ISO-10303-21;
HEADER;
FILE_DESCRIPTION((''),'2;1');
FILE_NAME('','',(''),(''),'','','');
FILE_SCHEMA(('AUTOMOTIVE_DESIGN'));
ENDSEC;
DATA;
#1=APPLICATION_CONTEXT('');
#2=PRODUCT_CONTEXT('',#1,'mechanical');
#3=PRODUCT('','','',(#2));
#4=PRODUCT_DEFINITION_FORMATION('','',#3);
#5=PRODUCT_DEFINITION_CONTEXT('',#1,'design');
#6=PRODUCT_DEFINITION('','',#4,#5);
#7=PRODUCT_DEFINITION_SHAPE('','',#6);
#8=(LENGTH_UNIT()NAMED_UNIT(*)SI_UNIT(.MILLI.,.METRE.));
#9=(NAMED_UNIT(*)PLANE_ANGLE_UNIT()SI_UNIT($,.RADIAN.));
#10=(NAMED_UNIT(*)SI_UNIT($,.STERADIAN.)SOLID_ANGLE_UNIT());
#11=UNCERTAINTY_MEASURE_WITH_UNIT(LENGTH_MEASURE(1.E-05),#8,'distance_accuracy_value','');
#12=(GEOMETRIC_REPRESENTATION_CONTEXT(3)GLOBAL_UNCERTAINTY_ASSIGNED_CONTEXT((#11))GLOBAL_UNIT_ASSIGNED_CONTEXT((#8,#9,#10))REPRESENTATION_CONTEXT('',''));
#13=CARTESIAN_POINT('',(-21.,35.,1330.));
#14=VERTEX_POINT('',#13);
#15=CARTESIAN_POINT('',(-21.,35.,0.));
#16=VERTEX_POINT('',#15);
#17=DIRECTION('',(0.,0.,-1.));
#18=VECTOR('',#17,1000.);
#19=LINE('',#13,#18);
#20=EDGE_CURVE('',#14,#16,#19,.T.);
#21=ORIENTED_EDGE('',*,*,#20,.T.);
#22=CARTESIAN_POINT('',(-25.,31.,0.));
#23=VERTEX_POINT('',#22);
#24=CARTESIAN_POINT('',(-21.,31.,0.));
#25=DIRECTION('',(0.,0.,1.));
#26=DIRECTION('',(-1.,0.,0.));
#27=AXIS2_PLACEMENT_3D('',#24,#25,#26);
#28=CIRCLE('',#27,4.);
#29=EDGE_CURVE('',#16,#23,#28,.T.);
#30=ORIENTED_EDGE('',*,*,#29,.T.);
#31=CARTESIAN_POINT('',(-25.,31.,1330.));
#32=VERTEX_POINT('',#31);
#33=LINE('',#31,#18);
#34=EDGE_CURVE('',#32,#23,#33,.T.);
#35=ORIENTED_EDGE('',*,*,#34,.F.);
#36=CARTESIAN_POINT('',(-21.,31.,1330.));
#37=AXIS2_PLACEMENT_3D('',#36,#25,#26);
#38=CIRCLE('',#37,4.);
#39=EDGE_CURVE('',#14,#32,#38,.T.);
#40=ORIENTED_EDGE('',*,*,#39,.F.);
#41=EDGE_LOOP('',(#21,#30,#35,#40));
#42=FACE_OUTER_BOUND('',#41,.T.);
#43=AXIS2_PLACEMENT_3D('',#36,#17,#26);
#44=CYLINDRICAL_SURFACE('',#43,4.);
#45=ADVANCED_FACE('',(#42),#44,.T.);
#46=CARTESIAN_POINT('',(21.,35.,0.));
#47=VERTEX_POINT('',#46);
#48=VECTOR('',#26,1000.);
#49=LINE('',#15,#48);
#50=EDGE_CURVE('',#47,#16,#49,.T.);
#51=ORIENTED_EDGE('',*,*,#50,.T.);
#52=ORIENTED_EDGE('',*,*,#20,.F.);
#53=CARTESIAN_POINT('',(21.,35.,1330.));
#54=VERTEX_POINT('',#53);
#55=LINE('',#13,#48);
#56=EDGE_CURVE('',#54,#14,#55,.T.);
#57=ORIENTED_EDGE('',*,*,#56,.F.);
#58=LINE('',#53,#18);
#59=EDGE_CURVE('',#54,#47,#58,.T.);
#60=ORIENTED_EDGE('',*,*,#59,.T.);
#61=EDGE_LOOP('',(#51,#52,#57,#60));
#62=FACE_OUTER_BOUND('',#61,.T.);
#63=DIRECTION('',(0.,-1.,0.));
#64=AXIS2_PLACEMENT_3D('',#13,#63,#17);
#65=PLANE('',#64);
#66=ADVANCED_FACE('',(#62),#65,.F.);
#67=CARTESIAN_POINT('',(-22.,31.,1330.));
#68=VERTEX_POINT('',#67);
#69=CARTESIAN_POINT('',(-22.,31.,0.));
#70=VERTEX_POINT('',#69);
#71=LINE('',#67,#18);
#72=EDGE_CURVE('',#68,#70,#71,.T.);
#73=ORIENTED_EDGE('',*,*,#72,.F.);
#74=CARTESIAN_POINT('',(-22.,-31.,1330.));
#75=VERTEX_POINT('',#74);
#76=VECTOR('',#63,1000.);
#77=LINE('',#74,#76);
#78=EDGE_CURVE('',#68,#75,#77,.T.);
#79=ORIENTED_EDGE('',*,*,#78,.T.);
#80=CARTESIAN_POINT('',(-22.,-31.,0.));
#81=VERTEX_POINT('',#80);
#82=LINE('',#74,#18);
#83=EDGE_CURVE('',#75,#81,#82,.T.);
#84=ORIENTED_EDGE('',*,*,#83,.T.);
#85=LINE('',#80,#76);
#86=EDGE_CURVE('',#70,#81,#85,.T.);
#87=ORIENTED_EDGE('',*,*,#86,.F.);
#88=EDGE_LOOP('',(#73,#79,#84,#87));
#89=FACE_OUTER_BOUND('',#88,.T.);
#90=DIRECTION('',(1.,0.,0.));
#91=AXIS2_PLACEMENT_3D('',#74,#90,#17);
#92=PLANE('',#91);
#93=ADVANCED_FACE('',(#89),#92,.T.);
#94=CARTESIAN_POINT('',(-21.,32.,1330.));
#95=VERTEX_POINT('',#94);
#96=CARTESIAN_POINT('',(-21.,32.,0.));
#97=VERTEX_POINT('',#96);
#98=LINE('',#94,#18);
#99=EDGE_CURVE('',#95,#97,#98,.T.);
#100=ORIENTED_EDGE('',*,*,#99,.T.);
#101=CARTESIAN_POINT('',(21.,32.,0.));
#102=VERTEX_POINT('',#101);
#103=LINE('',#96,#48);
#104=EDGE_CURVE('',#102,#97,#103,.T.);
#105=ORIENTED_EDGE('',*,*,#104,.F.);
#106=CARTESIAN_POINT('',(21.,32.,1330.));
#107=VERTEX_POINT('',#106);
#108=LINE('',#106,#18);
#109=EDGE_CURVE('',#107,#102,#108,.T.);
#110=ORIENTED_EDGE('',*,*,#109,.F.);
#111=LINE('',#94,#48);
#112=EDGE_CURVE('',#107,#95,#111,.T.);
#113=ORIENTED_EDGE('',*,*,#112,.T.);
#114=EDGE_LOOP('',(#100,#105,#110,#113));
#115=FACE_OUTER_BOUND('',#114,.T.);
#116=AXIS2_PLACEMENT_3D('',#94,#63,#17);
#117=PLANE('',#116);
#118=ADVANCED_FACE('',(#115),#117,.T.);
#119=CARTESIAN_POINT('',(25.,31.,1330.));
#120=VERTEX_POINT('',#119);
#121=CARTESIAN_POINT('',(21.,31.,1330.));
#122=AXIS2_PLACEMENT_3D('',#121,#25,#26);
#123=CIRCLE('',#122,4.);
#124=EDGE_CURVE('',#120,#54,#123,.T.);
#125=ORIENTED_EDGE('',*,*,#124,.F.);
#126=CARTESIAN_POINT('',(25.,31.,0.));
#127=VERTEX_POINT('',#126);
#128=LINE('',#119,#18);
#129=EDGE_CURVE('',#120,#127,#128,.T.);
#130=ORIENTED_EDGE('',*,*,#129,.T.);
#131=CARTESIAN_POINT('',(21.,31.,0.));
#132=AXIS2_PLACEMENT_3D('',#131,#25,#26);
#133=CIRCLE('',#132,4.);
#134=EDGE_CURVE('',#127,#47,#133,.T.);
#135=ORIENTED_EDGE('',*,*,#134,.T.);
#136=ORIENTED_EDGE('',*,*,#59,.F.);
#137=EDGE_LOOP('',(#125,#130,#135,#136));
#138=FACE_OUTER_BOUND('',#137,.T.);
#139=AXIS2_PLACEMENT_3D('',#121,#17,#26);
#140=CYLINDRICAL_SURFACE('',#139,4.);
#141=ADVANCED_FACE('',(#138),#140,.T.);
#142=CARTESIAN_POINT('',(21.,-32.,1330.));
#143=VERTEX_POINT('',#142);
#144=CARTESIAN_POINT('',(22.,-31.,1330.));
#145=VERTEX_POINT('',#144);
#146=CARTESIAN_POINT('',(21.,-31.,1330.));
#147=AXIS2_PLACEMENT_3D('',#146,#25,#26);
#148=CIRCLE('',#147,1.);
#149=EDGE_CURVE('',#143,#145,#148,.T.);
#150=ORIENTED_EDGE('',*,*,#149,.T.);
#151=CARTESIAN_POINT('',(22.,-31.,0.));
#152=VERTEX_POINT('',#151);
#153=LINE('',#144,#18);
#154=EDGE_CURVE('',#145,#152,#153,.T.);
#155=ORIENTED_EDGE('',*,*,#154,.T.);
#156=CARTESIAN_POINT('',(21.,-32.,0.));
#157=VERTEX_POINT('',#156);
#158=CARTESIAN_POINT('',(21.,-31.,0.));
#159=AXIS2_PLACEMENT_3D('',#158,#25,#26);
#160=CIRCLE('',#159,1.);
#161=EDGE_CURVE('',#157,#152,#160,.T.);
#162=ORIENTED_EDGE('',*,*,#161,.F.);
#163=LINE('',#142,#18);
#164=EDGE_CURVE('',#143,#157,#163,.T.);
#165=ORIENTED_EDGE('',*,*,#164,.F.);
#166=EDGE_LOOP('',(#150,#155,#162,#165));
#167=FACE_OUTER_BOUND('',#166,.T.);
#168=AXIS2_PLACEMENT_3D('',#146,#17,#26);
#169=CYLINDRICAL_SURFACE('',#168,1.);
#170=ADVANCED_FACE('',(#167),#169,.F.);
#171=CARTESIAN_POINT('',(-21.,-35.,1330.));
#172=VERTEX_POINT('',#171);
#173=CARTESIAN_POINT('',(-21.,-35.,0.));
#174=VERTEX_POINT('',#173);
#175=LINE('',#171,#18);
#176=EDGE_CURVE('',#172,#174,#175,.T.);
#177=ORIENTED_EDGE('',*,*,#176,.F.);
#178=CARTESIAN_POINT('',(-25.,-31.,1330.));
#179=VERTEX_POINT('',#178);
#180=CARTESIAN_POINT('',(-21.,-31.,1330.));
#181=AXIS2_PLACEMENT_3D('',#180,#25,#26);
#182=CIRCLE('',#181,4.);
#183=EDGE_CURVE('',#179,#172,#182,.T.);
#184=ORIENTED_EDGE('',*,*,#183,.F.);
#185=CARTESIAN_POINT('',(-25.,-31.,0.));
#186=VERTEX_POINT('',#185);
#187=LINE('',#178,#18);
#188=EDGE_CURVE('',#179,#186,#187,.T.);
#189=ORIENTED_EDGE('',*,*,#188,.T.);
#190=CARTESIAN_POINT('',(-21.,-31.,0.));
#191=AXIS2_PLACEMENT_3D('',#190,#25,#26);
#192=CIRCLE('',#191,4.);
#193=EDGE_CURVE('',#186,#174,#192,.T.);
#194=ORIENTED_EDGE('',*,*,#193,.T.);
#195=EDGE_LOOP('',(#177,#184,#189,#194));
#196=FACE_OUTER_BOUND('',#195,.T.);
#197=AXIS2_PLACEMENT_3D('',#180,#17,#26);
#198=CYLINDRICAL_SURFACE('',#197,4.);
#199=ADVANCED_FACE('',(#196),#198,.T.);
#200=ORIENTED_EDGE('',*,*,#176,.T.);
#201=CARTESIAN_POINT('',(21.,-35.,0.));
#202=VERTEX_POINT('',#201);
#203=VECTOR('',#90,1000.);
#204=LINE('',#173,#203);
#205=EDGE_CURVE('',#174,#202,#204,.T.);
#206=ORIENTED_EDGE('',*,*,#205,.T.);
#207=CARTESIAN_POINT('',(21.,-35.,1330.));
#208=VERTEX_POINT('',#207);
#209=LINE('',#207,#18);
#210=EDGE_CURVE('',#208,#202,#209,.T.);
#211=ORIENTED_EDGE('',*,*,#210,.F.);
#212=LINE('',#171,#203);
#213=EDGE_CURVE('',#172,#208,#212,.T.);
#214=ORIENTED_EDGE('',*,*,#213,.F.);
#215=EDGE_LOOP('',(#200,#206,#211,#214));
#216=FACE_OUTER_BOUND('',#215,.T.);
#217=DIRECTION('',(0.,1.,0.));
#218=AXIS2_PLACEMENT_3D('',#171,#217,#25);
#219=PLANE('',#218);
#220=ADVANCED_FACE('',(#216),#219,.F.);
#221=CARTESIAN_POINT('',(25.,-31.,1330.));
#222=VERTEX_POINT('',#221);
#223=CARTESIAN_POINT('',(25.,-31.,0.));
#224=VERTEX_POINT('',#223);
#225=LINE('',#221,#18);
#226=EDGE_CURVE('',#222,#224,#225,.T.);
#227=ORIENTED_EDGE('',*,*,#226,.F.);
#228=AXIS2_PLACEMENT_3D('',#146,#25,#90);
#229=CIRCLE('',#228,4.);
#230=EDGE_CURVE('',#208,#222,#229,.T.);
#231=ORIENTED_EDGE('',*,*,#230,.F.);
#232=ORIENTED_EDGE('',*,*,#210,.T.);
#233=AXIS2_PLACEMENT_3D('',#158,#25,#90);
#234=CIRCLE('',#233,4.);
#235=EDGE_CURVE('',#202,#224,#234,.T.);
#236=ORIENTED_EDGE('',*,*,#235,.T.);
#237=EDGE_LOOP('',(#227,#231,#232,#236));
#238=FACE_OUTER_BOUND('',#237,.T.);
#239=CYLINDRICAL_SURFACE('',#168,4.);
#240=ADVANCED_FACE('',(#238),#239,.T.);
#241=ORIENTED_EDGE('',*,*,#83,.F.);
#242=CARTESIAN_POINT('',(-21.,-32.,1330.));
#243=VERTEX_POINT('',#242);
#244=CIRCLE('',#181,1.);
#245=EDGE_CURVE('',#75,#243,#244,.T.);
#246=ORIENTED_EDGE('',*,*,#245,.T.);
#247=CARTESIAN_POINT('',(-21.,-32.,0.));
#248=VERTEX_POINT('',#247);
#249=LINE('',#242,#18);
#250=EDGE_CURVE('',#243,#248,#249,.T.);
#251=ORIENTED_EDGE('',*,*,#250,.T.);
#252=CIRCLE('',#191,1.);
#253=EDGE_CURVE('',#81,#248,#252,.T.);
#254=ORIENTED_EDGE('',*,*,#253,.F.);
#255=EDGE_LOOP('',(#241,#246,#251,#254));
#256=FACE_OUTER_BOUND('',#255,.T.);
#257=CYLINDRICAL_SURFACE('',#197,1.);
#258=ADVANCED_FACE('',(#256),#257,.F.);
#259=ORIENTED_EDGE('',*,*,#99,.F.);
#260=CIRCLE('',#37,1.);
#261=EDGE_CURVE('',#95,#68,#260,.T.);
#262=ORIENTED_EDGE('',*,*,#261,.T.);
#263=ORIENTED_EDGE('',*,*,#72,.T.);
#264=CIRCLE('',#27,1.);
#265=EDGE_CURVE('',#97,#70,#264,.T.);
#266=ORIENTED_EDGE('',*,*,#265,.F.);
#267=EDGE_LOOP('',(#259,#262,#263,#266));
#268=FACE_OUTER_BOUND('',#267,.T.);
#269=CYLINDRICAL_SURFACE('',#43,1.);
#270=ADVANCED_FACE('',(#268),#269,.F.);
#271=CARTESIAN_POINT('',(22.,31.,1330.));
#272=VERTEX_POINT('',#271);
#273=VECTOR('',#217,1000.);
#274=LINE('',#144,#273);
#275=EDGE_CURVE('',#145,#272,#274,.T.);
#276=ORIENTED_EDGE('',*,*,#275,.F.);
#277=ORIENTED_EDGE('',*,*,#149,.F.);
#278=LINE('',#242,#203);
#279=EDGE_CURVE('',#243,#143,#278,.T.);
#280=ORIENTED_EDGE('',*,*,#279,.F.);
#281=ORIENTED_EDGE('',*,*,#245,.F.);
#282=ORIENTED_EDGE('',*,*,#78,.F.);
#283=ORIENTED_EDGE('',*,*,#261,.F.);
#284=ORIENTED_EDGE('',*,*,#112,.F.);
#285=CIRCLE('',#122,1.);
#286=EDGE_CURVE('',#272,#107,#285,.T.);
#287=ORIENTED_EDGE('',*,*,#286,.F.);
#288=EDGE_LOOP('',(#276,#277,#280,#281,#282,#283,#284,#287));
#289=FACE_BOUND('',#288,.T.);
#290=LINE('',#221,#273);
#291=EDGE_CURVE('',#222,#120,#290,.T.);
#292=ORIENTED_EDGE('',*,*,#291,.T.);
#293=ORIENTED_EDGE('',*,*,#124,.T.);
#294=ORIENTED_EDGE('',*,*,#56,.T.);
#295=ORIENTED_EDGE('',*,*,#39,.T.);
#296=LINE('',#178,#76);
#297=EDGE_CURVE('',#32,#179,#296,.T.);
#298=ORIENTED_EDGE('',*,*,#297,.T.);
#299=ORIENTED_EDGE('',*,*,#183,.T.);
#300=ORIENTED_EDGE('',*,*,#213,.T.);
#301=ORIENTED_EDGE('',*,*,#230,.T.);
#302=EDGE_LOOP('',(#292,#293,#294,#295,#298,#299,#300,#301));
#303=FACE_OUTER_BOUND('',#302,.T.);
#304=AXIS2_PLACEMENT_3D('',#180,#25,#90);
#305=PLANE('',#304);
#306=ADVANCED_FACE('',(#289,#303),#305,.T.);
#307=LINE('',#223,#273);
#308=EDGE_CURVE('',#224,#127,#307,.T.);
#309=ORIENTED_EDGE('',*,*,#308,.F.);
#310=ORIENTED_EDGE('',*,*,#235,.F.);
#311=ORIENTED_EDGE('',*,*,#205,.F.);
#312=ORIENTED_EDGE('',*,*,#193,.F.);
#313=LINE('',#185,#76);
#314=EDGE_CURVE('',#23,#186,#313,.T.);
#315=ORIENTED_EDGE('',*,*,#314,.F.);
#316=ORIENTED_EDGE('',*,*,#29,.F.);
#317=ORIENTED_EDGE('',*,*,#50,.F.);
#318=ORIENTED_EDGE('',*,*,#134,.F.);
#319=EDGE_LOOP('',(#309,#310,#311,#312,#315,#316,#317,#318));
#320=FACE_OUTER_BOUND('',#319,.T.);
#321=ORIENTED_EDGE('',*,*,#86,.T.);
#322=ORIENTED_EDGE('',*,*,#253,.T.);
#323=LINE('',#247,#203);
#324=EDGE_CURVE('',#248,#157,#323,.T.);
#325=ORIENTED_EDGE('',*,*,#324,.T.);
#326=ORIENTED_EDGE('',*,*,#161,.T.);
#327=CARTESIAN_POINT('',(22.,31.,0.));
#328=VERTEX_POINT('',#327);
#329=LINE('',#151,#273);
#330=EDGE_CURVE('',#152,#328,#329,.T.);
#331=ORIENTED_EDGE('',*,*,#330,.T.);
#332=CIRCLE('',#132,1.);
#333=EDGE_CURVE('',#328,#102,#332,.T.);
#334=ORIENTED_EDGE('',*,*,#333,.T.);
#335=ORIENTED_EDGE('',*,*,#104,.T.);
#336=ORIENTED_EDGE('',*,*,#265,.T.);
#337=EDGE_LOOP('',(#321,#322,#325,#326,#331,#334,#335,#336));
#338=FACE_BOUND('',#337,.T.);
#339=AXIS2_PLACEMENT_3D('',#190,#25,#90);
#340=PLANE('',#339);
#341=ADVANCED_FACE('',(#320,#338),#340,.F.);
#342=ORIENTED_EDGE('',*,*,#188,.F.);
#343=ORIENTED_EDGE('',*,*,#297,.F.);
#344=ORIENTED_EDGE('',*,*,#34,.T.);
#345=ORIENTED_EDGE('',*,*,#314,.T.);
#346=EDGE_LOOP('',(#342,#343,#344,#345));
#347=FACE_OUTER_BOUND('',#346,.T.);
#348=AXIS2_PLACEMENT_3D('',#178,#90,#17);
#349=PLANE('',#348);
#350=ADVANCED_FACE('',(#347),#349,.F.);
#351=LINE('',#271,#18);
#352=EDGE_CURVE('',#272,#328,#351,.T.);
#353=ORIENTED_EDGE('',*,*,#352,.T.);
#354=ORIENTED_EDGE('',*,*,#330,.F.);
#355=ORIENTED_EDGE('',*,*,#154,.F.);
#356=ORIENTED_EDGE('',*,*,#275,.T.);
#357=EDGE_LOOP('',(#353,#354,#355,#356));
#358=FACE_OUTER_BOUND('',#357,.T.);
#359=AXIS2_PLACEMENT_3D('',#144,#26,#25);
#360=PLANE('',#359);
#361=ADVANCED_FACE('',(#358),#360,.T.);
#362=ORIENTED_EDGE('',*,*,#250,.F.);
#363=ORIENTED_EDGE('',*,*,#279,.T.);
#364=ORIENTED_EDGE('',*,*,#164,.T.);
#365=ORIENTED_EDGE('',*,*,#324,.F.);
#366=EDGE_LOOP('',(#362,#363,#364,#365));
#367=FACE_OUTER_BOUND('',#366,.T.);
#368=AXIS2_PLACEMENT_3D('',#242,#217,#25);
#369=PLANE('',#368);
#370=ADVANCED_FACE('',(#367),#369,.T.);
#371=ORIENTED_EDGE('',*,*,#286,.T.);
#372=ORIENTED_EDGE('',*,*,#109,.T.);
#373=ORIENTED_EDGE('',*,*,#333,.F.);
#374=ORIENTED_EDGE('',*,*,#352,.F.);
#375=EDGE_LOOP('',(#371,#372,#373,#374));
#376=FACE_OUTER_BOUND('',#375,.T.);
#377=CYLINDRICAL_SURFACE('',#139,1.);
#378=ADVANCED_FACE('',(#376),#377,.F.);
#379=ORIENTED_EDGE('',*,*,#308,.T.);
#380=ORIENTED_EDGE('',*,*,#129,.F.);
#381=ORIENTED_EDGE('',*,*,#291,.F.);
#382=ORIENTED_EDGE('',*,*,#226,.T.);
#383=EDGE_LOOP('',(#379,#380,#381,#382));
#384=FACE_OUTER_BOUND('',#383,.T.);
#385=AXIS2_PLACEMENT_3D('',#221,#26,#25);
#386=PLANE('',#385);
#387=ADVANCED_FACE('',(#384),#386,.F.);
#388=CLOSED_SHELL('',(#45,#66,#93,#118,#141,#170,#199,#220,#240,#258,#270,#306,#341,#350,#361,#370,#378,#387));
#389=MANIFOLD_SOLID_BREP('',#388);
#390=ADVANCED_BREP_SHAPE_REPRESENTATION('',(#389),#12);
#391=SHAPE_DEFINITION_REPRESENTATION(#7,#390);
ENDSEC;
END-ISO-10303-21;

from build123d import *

# Parameters (mm, degrees)
EXTRUDE_THIN1_DEPTH = 1330


with BuildPart() as part:
    # Sketch1 → Extrude-Thin1 (new body)
    with BuildSketch(Plane.XY):
        with BuildLine():
            Line((-25, 31), (-25, -31))
            ThreePointArc((-25, -31), (-23.828427125, -33.828427125), (-21, -35))
            Line((-21, -35), (21, -35))
            ThreePointArc((21, -35), (23.828427125, -33.828427125), (25, -31))
            Line((25, -31), (25, 31))
            ThreePointArc((25, 31), (23.828427125, 33.828427125), (21, 35))
            Line((21, 35), (-21, 35))
            ThreePointArc((-21, 35), (-23.828427125, 33.828427125), (-25, 31))
        make_face()
        with BuildLine():
            Line((-22, 31), (-22, -31))
            ThreePointArc((-22, -31), (-21.707106781, -31.707106781), (-21, -32))
            Line((-21, -32), (21, -32))
            ThreePointArc((21, -32), (21.707106781, -31.707106781), (22, -31))
            Line((22, -31), (22, 31))
            ThreePointArc((22, 31), (21.707106781, 31.707106781), (21, 32))
            Line((21, 32), (-21, 32))
            ThreePointArc((-21, 32), (-21.707106781, 31.707106781), (-22, 31))
        make_face(mode=Mode.SUBTRACT)
    extrude(amount=EXTRUDE_THIN1_DEPTH)


solid = part.part
